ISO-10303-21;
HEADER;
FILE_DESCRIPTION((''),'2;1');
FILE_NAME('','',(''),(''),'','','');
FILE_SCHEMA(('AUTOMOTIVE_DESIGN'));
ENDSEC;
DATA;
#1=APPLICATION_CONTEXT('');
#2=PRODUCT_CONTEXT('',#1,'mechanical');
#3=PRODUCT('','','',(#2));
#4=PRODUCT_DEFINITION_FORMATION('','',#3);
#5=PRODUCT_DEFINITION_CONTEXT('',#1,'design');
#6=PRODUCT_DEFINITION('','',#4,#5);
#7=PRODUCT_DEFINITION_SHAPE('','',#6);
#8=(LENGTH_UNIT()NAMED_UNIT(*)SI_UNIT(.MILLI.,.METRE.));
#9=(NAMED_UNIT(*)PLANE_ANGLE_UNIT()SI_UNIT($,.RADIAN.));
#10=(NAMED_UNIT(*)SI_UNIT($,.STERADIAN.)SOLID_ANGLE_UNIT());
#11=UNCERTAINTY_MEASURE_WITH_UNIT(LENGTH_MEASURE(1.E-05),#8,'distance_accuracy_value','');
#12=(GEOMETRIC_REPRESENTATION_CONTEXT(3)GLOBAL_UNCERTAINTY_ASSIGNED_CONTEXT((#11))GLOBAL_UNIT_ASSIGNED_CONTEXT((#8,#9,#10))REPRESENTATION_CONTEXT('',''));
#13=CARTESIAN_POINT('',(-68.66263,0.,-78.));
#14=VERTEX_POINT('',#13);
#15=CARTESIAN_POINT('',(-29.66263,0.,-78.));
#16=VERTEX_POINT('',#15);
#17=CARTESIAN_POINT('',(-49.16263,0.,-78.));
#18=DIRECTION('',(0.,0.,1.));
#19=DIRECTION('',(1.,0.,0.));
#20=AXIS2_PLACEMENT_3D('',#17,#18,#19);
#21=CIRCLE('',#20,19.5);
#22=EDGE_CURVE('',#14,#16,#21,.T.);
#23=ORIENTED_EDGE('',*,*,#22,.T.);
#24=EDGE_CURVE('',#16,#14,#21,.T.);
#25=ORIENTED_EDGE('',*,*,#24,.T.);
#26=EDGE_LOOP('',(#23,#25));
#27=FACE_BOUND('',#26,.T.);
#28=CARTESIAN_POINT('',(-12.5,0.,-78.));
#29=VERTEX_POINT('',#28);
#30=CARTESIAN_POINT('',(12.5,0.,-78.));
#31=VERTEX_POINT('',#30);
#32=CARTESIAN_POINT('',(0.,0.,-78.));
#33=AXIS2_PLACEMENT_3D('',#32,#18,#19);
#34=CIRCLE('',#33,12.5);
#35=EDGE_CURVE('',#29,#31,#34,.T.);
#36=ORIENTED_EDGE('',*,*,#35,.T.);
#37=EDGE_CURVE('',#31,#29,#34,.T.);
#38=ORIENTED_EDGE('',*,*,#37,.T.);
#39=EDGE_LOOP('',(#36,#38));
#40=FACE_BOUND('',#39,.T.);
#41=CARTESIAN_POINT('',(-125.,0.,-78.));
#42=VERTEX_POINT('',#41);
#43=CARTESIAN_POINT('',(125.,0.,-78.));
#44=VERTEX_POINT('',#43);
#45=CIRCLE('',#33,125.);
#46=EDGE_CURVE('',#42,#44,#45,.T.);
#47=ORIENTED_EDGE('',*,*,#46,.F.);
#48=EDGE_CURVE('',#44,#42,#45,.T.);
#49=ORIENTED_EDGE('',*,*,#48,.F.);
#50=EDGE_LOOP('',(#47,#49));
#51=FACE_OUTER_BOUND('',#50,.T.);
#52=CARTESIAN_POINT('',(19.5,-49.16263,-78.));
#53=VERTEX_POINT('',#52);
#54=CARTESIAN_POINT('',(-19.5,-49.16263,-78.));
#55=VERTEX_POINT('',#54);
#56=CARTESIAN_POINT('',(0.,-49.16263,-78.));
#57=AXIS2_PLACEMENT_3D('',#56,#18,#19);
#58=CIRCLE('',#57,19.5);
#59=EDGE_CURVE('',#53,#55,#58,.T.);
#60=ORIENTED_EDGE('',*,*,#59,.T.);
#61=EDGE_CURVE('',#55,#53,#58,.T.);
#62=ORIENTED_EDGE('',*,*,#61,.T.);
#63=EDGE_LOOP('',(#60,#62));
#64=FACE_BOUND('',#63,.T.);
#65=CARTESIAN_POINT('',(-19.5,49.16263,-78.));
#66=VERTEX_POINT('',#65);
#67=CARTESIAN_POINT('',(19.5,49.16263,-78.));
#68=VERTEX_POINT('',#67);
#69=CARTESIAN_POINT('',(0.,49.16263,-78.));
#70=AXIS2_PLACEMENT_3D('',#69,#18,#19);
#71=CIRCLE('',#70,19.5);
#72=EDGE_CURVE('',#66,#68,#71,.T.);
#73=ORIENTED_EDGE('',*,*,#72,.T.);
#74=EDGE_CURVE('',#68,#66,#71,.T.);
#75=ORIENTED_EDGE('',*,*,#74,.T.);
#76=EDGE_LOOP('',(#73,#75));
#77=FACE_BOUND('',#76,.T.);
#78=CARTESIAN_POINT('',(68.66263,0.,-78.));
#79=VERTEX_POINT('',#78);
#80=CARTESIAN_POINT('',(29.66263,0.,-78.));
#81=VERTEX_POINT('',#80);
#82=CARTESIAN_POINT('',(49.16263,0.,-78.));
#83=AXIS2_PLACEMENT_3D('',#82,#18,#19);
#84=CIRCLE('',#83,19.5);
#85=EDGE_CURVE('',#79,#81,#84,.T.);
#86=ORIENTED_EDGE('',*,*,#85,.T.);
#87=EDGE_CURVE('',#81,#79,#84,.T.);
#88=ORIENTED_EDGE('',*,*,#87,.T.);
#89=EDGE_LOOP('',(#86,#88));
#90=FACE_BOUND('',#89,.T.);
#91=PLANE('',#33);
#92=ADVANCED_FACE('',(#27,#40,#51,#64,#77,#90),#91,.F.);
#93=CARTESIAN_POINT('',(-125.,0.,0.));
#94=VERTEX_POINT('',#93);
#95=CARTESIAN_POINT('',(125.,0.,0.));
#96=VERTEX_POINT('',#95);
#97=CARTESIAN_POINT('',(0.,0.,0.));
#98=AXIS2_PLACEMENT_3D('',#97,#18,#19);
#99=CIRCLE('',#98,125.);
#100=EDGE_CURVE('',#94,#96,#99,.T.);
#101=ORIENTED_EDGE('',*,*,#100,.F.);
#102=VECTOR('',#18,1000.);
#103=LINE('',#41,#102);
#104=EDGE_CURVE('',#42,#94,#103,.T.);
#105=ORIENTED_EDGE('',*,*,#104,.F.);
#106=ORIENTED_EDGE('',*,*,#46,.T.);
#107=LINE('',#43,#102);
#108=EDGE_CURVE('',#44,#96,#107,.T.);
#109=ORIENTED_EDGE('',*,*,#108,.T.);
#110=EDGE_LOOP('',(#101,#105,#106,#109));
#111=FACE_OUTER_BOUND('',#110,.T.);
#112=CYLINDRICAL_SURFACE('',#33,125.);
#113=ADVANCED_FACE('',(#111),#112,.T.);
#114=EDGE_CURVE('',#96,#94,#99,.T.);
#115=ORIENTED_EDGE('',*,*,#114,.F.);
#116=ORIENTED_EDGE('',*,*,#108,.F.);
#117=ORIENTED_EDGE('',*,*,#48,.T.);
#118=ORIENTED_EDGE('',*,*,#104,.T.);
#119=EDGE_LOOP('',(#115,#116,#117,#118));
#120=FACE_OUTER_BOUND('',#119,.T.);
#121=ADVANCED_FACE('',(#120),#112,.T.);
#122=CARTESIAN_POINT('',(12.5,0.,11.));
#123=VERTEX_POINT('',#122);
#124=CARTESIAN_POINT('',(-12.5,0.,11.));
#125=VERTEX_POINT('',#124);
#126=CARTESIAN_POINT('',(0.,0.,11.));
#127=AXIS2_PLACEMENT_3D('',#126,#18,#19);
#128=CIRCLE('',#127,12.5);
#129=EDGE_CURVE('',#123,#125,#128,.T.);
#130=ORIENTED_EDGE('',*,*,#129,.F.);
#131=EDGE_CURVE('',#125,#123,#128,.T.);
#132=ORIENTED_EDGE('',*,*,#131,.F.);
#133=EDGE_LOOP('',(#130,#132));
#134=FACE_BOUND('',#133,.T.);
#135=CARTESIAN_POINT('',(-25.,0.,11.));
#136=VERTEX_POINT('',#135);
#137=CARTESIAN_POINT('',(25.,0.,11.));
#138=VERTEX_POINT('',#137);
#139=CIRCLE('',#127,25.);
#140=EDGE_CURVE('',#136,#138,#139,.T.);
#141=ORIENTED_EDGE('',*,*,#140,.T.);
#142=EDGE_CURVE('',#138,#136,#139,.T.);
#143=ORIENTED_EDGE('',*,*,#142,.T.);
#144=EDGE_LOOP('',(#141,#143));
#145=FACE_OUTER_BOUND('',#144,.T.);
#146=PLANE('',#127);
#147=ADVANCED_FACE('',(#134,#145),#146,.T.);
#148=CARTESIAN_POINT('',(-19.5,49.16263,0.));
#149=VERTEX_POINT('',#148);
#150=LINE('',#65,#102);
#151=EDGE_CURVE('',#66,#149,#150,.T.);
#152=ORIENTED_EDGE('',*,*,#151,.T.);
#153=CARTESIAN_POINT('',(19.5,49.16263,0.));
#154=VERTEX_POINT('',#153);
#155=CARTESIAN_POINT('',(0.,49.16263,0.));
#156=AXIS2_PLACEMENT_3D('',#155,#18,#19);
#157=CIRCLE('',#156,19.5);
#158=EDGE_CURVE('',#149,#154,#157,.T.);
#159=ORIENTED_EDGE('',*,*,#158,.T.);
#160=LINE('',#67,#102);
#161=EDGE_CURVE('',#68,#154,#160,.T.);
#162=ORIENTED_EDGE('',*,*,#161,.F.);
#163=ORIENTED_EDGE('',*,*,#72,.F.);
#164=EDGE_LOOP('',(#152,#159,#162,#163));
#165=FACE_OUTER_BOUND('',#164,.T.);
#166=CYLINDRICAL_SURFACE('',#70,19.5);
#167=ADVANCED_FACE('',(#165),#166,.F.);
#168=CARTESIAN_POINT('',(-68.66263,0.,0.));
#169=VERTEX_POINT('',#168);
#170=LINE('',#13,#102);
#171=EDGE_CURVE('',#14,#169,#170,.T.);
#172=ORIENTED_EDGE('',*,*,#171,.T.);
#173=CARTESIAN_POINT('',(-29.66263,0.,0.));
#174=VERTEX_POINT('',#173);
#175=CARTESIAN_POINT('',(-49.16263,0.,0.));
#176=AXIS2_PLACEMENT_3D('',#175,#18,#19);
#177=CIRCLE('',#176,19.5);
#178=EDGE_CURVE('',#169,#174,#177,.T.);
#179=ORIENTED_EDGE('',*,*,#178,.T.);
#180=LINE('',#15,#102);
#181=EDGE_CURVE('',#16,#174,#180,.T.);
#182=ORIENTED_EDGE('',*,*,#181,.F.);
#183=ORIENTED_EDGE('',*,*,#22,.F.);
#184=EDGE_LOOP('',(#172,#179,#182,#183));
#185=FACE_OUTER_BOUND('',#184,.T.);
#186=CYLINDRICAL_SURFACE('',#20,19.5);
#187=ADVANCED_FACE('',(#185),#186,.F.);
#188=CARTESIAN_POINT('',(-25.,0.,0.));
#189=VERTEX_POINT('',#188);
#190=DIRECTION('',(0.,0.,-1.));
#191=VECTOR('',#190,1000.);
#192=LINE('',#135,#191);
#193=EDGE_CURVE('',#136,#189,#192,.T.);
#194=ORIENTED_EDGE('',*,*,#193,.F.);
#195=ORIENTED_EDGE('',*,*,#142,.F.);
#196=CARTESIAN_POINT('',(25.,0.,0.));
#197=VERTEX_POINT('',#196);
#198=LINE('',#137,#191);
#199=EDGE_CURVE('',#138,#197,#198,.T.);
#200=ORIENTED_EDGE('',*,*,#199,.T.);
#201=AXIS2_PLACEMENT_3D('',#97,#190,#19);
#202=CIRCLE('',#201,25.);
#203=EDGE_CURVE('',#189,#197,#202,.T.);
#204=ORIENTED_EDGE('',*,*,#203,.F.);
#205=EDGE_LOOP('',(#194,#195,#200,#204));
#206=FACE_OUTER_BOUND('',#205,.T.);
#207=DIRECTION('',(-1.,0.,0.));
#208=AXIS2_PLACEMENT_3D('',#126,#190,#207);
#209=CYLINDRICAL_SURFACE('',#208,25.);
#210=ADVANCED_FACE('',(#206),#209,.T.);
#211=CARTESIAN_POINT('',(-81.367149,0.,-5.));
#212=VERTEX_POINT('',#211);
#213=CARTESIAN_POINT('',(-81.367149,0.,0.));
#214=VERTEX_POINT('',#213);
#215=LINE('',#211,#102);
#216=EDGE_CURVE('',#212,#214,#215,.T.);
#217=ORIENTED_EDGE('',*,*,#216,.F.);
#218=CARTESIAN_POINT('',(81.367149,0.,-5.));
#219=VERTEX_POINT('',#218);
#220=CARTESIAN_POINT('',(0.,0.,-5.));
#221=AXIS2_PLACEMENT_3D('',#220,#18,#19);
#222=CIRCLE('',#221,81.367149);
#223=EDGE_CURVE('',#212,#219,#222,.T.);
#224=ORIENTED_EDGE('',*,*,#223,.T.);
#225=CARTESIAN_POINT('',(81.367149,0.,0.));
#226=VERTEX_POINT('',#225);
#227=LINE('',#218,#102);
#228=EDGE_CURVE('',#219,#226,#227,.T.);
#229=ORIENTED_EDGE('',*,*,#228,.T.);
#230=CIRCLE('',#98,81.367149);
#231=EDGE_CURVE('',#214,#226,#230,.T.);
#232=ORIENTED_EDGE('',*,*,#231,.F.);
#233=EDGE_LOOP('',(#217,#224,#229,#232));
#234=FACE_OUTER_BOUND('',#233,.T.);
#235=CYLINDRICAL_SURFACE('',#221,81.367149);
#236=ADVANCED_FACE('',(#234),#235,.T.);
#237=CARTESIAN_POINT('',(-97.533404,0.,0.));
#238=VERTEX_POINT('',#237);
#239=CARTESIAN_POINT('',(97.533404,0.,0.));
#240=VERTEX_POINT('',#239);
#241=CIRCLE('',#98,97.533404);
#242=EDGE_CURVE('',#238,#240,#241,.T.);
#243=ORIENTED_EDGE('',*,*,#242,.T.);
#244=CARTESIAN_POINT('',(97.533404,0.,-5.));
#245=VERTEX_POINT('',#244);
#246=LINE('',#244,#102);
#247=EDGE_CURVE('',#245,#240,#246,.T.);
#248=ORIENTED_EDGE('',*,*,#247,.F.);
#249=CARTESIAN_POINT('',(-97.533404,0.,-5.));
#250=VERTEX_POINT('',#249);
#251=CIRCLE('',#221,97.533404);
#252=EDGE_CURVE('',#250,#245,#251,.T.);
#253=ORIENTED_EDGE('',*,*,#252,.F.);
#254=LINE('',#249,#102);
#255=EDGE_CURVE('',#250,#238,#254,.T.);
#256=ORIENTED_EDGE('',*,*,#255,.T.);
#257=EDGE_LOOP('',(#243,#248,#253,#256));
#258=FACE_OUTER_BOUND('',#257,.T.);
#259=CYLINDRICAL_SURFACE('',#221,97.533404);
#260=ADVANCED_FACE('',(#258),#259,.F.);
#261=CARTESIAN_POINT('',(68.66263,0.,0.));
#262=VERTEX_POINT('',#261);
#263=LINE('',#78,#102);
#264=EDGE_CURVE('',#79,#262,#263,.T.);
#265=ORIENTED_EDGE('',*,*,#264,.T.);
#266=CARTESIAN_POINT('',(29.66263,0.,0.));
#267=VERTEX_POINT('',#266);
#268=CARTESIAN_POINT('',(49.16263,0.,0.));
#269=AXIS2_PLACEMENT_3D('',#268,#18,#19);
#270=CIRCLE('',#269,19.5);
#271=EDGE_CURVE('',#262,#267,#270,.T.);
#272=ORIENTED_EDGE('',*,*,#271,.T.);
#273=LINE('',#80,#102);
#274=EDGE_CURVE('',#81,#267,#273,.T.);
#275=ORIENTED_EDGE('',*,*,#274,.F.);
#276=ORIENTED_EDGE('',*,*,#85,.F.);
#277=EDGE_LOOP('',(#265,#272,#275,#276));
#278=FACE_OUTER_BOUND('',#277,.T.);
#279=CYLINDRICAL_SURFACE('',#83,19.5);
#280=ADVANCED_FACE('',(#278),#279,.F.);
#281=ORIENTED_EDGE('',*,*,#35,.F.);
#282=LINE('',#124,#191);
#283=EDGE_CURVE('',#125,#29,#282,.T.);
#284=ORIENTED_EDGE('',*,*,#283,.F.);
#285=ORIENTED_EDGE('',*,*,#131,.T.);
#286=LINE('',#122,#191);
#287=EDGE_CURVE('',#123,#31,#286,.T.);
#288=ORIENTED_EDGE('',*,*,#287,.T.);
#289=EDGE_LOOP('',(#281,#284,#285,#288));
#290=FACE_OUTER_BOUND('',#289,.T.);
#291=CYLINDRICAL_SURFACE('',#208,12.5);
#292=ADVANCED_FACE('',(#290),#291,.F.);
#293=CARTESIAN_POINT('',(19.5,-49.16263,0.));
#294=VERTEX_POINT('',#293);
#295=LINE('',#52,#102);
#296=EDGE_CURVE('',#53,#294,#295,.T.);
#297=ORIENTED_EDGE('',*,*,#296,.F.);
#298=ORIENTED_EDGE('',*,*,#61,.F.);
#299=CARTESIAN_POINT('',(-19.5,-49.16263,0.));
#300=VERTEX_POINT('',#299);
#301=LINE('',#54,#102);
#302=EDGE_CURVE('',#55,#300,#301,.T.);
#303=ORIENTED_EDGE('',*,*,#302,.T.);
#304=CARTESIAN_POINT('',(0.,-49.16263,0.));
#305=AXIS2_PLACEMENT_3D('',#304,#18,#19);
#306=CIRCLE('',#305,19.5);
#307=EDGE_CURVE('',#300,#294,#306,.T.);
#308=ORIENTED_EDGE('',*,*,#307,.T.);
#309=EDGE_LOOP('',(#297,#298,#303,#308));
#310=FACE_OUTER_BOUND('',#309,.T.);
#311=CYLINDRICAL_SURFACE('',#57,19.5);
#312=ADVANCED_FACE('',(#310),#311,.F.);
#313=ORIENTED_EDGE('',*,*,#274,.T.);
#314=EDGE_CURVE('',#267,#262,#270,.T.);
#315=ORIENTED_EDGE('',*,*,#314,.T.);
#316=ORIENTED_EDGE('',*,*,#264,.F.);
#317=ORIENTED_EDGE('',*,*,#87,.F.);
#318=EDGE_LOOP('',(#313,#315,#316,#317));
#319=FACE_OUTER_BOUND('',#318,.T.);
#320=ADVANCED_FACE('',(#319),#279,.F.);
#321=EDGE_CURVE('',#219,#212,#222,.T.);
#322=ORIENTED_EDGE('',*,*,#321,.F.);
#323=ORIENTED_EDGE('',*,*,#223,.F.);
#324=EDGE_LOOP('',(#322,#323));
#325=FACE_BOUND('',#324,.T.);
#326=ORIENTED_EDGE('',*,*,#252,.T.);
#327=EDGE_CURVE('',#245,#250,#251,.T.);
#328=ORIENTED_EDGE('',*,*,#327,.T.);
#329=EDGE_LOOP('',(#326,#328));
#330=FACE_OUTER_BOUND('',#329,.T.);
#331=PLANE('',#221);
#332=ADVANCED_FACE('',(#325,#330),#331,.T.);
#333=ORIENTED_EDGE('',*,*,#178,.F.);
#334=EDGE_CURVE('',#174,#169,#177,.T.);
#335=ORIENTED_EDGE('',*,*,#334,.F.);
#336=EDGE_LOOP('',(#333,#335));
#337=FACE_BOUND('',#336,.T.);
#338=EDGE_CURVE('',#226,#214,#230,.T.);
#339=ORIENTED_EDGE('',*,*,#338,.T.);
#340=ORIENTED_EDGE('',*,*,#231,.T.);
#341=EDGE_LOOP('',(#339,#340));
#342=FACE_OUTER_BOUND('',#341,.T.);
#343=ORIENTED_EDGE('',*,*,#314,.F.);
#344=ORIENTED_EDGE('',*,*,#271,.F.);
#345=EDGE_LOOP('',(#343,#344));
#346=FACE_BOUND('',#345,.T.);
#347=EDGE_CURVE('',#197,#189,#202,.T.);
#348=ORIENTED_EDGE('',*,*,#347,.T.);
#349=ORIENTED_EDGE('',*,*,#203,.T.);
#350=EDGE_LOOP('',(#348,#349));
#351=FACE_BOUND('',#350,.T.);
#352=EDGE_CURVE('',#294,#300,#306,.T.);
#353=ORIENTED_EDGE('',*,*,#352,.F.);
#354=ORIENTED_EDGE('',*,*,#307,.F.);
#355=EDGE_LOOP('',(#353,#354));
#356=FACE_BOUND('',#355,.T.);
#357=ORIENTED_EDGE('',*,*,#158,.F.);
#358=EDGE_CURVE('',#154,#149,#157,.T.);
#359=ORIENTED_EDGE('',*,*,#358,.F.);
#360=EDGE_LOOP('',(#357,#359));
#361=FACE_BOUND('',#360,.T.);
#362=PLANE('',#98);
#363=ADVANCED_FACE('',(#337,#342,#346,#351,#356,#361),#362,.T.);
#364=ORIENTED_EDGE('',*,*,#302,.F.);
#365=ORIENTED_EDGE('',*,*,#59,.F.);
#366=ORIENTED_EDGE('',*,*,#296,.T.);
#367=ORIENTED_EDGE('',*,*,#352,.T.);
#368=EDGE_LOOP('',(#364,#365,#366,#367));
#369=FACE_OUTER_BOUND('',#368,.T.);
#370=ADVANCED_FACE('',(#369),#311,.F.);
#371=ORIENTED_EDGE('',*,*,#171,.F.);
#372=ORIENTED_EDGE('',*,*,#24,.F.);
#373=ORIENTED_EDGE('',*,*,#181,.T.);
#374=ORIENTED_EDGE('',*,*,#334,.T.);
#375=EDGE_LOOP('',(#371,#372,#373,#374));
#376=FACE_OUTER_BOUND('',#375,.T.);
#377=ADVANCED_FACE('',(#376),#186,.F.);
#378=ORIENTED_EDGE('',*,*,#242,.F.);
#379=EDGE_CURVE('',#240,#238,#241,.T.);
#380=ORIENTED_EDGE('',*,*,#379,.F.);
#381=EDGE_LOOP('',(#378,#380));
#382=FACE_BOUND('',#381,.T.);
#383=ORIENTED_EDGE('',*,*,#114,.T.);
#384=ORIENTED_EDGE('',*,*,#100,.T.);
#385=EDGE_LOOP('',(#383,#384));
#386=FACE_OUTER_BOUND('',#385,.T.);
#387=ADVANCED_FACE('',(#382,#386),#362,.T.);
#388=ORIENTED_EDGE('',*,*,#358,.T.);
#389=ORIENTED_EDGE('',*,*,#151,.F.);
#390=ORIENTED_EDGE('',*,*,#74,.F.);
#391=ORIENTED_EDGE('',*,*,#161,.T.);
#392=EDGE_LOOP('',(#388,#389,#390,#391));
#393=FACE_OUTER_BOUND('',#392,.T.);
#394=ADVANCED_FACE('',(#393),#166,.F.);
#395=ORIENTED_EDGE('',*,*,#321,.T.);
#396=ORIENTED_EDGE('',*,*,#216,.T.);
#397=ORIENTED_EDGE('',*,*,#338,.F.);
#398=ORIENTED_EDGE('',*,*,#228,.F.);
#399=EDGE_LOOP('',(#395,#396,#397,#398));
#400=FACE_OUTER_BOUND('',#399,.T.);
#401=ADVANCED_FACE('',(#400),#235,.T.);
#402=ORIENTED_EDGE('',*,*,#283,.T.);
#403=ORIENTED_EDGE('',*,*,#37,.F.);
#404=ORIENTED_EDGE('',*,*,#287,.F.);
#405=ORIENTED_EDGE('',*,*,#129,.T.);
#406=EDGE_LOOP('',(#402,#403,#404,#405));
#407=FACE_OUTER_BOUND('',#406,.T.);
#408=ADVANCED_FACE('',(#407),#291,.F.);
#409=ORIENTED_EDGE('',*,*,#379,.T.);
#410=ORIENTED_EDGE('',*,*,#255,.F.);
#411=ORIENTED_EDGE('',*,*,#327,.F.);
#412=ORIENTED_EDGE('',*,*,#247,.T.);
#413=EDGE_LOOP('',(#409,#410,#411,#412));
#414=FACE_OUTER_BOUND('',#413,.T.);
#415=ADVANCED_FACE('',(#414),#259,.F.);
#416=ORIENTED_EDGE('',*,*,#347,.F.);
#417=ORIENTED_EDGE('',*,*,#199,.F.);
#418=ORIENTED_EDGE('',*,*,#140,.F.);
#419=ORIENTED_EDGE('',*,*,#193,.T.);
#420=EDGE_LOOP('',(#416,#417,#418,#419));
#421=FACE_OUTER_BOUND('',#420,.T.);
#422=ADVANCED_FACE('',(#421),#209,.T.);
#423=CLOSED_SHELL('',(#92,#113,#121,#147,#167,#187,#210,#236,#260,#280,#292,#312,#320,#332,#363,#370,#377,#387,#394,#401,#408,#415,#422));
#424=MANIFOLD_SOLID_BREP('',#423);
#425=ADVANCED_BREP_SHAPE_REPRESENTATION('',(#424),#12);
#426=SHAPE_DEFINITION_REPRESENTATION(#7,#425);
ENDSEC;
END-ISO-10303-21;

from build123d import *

# Parameters (mm, degrees)
WHEEL_DISC_SKETCH_R        = 125
WHEEL_DISC_250_DEPTH       = 78
FACE_RECESS_SKETCH_R       = 97.533404225
FACE_RECESS_SKETCH_R_2     = 81.367148925
FACE_RECESS_5MM_DEPTH      = 5
LIGHTENING_HOLE_1_SKETCH_R = 19.5
LIGHTENING_HOLE_1_39_DEPTH = 78
LIGHTENING_HOLE_2_SKETCH_R = 19.5
LIGHTENING_HOLE_2_39_DEPTH = 78
LIGHTENING_HOLE_3_SKETCH_R = 19.5
LIGHTENING_HOLE_3_39_DEPTH = 78
LIGHTENING_HOLE_4_SKETCH_R = 19.5
LIGHTENING_HOLE_4_39_DEPTH = 78
HUB_BOSS_SKETCH_R          = 25
HUB_BOSS_SKETCH_R_2        = 12.5
HUB_BOSS_50_DEPTH          = 16
CENTRE_START               = -78
CENTRE_CUT_SKETCH_R        = 12.5
CENTRE_CUT_DEPTH           = 78


with BuildPart() as part:
    # Wheel Disc Sketch → Wheel Disc Ø250 (new body)
    with BuildSketch(Plane.XY):
        Circle(WHEEL_DISC_SKETCH_R)
    extrude(amount=-WHEEL_DISC_250_DEPTH)

    # Face Recess Sketch → Face Recess 5mm (cut)
    with BuildSketch(Plane.XY):
        Circle(FACE_RECESS_SKETCH_R)
        Circle(FACE_RECESS_SKETCH_R_2, mode=Mode.SUBTRACT)
    extrude(amount=-FACE_RECESS_5MM_DEPTH, mode=Mode.SUBTRACT)

    # Lightening Hole 1 Sketch → Lightening Hole 1 Ø39 (cut)
    with BuildSketch(Plane.XY):
        with Locations((0, 49.162629863)):
            Circle(LIGHTENING_HOLE_1_SKETCH_R)
    extrude(amount=-LIGHTENING_HOLE_1_39_DEPTH, mode=Mode.SUBTRACT)

    # Lightening Hole 2 Sketch → Lightening Hole 2 Ø39 (cut)
    with BuildSketch(Plane.XY):
        with Locations((49.162629863, 0)):
            Circle(LIGHTENING_HOLE_2_SKETCH_R)
    extrude(amount=-LIGHTENING_HOLE_2_39_DEPTH, mode=Mode.SUBTRACT)

    # Lightening Hole 3 Sketch → Lightening Hole 3 Ø39 (cut)
    with BuildSketch(Plane.XY):
        with Locations((0, -49.162629863)):
            Circle(LIGHTENING_HOLE_3_SKETCH_R)
    extrude(amount=-LIGHTENING_HOLE_3_39_DEPTH, mode=Mode.SUBTRACT)

    # Lightening Hole 4 Sketch → Lightening Hole 4 Ø39 (cut)
    with BuildSketch(Plane.XY):
        with Locations((-49.162629863, 0)):
            Circle(LIGHTENING_HOLE_4_SKETCH_R)
    extrude(amount=-LIGHTENING_HOLE_4_39_DEPTH, mode=Mode.SUBTRACT)

    # Hub Boss Sketch → Hub Boss Ø50 (add)
    with BuildSketch(Plane.XY.offset(-5)):
        Circle(HUB_BOSS_SKETCH_R)
        Circle(HUB_BOSS_SKETCH_R_2, mode=Mode.SUBTRACT)
    extrude(amount=HUB_BOSS_50_DEPTH)

    # Centre Cut Sketch → Centre Cut (cut)
    with BuildSketch(Plane.XY.offset(CENTRE_START)):
        Circle(CENTRE_CUT_SKETCH_R)
    extrude(amount=CENTRE_CUT_DEPTH, mode=Mode.SUBTRACT)


solid = part.part
